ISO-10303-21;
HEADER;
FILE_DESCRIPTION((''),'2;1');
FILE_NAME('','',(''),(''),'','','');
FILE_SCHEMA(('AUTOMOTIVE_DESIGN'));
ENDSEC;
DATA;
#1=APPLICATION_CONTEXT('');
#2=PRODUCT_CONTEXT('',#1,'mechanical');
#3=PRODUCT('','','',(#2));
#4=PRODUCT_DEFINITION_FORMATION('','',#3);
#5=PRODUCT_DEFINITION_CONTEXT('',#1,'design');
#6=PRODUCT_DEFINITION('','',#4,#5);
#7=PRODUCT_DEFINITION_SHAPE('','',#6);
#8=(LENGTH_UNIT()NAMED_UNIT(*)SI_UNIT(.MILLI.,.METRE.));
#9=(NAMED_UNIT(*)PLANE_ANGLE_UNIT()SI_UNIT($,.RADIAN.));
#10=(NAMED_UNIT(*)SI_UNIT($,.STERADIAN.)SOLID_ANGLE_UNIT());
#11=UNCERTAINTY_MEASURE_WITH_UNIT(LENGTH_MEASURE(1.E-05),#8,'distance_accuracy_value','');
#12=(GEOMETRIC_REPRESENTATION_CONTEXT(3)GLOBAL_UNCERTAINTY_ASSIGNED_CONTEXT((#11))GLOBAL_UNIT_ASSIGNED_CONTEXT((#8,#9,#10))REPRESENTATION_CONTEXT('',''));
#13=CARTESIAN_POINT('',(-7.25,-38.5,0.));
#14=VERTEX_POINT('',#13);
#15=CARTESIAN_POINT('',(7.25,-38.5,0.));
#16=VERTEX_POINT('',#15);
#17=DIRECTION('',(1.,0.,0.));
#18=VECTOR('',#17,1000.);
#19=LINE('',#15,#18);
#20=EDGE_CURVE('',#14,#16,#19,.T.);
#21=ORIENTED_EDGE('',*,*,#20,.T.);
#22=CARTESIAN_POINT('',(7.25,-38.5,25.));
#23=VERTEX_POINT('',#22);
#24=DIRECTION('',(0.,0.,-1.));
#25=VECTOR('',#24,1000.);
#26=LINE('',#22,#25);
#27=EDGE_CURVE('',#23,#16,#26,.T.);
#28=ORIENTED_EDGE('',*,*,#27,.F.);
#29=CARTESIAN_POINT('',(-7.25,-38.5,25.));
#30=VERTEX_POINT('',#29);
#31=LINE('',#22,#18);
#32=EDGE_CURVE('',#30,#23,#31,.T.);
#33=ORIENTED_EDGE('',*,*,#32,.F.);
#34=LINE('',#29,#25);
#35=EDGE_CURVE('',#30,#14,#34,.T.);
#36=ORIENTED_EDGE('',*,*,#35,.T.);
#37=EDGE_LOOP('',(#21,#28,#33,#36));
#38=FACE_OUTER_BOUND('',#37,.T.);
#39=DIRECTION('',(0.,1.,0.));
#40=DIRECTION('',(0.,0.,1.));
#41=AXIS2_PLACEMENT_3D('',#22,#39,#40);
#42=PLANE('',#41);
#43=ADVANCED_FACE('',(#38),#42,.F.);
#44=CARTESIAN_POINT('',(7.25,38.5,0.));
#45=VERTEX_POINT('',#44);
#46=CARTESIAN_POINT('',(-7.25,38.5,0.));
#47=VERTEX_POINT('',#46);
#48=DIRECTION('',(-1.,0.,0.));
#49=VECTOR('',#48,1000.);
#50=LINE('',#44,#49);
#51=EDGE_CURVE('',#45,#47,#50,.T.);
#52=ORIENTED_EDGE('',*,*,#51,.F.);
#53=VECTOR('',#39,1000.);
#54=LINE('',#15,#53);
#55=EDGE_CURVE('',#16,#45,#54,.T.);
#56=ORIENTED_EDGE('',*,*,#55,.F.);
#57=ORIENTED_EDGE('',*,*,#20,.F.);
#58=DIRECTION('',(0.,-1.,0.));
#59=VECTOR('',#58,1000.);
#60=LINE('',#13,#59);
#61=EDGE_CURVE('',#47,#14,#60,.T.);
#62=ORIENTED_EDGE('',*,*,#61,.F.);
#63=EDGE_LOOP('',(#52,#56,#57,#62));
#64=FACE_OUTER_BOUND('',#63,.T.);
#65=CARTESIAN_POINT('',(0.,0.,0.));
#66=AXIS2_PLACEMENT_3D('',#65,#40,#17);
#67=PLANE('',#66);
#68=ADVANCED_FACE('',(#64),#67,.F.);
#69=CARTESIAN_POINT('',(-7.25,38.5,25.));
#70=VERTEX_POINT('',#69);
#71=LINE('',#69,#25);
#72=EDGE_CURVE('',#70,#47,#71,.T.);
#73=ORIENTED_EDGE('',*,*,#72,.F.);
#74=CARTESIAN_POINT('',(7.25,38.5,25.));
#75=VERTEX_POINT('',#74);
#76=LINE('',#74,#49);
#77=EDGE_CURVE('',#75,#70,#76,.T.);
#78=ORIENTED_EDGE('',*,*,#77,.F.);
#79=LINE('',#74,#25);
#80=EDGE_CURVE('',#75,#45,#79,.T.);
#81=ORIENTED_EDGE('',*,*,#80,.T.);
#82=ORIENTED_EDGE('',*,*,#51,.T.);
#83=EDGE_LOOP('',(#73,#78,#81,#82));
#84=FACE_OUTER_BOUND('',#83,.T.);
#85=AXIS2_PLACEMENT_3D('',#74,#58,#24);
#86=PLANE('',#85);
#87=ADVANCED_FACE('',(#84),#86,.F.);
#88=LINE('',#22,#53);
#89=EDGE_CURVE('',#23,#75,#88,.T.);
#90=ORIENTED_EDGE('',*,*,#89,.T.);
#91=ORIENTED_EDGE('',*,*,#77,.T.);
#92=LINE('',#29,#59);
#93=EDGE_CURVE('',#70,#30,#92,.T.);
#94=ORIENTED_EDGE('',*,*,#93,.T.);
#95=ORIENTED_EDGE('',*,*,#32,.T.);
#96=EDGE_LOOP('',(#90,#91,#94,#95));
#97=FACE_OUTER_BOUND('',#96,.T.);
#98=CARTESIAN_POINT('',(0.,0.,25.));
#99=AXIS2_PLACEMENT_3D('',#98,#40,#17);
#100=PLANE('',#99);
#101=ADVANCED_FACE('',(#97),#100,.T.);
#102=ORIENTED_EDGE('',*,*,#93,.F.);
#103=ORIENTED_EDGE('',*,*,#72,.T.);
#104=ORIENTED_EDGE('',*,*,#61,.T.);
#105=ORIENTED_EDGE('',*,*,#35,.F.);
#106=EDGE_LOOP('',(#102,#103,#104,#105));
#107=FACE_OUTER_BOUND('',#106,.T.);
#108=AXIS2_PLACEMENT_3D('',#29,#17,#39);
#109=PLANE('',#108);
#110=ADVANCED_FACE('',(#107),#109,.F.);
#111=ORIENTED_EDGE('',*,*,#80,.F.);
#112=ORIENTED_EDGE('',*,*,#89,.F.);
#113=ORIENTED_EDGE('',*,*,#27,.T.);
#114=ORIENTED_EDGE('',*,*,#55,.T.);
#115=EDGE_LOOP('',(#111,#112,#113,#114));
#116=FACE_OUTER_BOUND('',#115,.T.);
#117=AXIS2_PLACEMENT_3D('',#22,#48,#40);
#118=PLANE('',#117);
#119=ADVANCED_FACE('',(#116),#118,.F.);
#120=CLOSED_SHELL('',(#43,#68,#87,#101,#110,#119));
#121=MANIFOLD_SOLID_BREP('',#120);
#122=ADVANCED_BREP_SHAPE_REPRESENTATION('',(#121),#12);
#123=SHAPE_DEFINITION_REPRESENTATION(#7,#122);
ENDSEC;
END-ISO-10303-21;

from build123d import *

# Parameters (mm, degrees)
SKETCH1_W           = 14.5
SKETCH1_H           = 77
BOSS_EXTRUDE1_DEPTH = 25


with BuildPart() as part:
    # Sketch1 → Boss-Extrude1 (new body)
    with BuildSketch(Plane.XY):
        Rectangle(SKETCH1_W, SKETCH1_H)
    extrude(amount=BOSS_EXTRUDE1_DEPTH)


solid = part.part
